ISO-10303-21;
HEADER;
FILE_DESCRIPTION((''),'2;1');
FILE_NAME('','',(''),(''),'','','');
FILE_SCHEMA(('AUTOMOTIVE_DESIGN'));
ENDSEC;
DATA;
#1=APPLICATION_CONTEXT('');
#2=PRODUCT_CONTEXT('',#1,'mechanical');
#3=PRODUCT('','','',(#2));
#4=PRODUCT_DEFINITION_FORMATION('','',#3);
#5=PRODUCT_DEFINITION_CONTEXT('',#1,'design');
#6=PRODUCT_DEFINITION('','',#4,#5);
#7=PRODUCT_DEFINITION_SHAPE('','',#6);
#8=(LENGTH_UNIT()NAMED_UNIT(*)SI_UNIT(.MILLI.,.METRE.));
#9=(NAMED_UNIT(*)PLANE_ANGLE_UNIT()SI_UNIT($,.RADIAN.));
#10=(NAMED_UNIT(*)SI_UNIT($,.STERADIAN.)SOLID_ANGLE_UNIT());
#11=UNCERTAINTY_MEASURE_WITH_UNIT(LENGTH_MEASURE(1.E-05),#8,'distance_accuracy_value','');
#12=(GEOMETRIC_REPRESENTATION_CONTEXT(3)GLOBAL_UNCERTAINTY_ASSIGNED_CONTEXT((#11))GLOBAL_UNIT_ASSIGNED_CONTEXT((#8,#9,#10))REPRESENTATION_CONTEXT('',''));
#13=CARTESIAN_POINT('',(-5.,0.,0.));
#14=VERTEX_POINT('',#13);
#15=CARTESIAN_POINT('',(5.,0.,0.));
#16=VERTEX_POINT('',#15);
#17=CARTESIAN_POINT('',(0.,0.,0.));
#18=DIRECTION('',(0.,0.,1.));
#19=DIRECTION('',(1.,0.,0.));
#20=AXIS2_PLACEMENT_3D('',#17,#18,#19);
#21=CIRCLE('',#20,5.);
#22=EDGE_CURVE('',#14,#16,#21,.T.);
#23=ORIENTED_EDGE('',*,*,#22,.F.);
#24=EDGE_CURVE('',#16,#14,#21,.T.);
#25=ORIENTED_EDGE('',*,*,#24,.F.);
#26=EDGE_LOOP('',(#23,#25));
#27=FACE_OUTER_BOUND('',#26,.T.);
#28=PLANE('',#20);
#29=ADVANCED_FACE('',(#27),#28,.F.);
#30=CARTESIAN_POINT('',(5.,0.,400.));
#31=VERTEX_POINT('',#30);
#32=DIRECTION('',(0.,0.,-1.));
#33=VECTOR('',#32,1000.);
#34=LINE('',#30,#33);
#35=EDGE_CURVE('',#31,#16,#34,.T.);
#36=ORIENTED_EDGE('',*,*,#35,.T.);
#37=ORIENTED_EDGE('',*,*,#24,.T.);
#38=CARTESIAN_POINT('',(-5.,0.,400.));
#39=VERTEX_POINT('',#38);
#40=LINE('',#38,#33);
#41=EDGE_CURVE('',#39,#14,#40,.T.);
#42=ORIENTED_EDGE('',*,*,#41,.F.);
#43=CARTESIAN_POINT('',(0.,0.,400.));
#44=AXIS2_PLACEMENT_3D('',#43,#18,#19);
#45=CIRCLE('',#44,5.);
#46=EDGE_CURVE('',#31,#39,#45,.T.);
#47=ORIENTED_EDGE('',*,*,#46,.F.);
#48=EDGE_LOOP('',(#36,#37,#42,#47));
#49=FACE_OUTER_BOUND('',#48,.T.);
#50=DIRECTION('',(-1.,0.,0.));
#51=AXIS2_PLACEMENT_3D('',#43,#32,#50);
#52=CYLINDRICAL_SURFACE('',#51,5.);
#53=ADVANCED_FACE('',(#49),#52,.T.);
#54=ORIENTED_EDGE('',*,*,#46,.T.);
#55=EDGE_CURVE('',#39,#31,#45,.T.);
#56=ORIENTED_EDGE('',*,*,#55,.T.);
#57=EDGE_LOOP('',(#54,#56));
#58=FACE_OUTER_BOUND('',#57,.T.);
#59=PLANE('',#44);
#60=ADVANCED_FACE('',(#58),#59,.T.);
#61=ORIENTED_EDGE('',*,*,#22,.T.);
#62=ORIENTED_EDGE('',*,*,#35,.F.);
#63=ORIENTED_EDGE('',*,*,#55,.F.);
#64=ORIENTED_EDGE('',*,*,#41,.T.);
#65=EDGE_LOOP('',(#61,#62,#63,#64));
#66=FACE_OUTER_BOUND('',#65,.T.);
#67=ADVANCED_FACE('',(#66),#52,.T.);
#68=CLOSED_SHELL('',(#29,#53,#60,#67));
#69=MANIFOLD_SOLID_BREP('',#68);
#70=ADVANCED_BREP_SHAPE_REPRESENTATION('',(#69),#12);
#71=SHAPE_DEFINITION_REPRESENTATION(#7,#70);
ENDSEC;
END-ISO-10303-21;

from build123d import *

# Parameters (mm, degrees)
SKETCH_1_R      = 5
EXTRUDE_1_DEPTH = 400


with BuildPart() as part:
    # 草图1 → 凸台-拉伸1 (new body)
    with BuildSketch(Plane.XY):
        Circle(SKETCH_1_R)
    extrude(amount=EXTRUDE_1_DEPTH)


solid = part.part
